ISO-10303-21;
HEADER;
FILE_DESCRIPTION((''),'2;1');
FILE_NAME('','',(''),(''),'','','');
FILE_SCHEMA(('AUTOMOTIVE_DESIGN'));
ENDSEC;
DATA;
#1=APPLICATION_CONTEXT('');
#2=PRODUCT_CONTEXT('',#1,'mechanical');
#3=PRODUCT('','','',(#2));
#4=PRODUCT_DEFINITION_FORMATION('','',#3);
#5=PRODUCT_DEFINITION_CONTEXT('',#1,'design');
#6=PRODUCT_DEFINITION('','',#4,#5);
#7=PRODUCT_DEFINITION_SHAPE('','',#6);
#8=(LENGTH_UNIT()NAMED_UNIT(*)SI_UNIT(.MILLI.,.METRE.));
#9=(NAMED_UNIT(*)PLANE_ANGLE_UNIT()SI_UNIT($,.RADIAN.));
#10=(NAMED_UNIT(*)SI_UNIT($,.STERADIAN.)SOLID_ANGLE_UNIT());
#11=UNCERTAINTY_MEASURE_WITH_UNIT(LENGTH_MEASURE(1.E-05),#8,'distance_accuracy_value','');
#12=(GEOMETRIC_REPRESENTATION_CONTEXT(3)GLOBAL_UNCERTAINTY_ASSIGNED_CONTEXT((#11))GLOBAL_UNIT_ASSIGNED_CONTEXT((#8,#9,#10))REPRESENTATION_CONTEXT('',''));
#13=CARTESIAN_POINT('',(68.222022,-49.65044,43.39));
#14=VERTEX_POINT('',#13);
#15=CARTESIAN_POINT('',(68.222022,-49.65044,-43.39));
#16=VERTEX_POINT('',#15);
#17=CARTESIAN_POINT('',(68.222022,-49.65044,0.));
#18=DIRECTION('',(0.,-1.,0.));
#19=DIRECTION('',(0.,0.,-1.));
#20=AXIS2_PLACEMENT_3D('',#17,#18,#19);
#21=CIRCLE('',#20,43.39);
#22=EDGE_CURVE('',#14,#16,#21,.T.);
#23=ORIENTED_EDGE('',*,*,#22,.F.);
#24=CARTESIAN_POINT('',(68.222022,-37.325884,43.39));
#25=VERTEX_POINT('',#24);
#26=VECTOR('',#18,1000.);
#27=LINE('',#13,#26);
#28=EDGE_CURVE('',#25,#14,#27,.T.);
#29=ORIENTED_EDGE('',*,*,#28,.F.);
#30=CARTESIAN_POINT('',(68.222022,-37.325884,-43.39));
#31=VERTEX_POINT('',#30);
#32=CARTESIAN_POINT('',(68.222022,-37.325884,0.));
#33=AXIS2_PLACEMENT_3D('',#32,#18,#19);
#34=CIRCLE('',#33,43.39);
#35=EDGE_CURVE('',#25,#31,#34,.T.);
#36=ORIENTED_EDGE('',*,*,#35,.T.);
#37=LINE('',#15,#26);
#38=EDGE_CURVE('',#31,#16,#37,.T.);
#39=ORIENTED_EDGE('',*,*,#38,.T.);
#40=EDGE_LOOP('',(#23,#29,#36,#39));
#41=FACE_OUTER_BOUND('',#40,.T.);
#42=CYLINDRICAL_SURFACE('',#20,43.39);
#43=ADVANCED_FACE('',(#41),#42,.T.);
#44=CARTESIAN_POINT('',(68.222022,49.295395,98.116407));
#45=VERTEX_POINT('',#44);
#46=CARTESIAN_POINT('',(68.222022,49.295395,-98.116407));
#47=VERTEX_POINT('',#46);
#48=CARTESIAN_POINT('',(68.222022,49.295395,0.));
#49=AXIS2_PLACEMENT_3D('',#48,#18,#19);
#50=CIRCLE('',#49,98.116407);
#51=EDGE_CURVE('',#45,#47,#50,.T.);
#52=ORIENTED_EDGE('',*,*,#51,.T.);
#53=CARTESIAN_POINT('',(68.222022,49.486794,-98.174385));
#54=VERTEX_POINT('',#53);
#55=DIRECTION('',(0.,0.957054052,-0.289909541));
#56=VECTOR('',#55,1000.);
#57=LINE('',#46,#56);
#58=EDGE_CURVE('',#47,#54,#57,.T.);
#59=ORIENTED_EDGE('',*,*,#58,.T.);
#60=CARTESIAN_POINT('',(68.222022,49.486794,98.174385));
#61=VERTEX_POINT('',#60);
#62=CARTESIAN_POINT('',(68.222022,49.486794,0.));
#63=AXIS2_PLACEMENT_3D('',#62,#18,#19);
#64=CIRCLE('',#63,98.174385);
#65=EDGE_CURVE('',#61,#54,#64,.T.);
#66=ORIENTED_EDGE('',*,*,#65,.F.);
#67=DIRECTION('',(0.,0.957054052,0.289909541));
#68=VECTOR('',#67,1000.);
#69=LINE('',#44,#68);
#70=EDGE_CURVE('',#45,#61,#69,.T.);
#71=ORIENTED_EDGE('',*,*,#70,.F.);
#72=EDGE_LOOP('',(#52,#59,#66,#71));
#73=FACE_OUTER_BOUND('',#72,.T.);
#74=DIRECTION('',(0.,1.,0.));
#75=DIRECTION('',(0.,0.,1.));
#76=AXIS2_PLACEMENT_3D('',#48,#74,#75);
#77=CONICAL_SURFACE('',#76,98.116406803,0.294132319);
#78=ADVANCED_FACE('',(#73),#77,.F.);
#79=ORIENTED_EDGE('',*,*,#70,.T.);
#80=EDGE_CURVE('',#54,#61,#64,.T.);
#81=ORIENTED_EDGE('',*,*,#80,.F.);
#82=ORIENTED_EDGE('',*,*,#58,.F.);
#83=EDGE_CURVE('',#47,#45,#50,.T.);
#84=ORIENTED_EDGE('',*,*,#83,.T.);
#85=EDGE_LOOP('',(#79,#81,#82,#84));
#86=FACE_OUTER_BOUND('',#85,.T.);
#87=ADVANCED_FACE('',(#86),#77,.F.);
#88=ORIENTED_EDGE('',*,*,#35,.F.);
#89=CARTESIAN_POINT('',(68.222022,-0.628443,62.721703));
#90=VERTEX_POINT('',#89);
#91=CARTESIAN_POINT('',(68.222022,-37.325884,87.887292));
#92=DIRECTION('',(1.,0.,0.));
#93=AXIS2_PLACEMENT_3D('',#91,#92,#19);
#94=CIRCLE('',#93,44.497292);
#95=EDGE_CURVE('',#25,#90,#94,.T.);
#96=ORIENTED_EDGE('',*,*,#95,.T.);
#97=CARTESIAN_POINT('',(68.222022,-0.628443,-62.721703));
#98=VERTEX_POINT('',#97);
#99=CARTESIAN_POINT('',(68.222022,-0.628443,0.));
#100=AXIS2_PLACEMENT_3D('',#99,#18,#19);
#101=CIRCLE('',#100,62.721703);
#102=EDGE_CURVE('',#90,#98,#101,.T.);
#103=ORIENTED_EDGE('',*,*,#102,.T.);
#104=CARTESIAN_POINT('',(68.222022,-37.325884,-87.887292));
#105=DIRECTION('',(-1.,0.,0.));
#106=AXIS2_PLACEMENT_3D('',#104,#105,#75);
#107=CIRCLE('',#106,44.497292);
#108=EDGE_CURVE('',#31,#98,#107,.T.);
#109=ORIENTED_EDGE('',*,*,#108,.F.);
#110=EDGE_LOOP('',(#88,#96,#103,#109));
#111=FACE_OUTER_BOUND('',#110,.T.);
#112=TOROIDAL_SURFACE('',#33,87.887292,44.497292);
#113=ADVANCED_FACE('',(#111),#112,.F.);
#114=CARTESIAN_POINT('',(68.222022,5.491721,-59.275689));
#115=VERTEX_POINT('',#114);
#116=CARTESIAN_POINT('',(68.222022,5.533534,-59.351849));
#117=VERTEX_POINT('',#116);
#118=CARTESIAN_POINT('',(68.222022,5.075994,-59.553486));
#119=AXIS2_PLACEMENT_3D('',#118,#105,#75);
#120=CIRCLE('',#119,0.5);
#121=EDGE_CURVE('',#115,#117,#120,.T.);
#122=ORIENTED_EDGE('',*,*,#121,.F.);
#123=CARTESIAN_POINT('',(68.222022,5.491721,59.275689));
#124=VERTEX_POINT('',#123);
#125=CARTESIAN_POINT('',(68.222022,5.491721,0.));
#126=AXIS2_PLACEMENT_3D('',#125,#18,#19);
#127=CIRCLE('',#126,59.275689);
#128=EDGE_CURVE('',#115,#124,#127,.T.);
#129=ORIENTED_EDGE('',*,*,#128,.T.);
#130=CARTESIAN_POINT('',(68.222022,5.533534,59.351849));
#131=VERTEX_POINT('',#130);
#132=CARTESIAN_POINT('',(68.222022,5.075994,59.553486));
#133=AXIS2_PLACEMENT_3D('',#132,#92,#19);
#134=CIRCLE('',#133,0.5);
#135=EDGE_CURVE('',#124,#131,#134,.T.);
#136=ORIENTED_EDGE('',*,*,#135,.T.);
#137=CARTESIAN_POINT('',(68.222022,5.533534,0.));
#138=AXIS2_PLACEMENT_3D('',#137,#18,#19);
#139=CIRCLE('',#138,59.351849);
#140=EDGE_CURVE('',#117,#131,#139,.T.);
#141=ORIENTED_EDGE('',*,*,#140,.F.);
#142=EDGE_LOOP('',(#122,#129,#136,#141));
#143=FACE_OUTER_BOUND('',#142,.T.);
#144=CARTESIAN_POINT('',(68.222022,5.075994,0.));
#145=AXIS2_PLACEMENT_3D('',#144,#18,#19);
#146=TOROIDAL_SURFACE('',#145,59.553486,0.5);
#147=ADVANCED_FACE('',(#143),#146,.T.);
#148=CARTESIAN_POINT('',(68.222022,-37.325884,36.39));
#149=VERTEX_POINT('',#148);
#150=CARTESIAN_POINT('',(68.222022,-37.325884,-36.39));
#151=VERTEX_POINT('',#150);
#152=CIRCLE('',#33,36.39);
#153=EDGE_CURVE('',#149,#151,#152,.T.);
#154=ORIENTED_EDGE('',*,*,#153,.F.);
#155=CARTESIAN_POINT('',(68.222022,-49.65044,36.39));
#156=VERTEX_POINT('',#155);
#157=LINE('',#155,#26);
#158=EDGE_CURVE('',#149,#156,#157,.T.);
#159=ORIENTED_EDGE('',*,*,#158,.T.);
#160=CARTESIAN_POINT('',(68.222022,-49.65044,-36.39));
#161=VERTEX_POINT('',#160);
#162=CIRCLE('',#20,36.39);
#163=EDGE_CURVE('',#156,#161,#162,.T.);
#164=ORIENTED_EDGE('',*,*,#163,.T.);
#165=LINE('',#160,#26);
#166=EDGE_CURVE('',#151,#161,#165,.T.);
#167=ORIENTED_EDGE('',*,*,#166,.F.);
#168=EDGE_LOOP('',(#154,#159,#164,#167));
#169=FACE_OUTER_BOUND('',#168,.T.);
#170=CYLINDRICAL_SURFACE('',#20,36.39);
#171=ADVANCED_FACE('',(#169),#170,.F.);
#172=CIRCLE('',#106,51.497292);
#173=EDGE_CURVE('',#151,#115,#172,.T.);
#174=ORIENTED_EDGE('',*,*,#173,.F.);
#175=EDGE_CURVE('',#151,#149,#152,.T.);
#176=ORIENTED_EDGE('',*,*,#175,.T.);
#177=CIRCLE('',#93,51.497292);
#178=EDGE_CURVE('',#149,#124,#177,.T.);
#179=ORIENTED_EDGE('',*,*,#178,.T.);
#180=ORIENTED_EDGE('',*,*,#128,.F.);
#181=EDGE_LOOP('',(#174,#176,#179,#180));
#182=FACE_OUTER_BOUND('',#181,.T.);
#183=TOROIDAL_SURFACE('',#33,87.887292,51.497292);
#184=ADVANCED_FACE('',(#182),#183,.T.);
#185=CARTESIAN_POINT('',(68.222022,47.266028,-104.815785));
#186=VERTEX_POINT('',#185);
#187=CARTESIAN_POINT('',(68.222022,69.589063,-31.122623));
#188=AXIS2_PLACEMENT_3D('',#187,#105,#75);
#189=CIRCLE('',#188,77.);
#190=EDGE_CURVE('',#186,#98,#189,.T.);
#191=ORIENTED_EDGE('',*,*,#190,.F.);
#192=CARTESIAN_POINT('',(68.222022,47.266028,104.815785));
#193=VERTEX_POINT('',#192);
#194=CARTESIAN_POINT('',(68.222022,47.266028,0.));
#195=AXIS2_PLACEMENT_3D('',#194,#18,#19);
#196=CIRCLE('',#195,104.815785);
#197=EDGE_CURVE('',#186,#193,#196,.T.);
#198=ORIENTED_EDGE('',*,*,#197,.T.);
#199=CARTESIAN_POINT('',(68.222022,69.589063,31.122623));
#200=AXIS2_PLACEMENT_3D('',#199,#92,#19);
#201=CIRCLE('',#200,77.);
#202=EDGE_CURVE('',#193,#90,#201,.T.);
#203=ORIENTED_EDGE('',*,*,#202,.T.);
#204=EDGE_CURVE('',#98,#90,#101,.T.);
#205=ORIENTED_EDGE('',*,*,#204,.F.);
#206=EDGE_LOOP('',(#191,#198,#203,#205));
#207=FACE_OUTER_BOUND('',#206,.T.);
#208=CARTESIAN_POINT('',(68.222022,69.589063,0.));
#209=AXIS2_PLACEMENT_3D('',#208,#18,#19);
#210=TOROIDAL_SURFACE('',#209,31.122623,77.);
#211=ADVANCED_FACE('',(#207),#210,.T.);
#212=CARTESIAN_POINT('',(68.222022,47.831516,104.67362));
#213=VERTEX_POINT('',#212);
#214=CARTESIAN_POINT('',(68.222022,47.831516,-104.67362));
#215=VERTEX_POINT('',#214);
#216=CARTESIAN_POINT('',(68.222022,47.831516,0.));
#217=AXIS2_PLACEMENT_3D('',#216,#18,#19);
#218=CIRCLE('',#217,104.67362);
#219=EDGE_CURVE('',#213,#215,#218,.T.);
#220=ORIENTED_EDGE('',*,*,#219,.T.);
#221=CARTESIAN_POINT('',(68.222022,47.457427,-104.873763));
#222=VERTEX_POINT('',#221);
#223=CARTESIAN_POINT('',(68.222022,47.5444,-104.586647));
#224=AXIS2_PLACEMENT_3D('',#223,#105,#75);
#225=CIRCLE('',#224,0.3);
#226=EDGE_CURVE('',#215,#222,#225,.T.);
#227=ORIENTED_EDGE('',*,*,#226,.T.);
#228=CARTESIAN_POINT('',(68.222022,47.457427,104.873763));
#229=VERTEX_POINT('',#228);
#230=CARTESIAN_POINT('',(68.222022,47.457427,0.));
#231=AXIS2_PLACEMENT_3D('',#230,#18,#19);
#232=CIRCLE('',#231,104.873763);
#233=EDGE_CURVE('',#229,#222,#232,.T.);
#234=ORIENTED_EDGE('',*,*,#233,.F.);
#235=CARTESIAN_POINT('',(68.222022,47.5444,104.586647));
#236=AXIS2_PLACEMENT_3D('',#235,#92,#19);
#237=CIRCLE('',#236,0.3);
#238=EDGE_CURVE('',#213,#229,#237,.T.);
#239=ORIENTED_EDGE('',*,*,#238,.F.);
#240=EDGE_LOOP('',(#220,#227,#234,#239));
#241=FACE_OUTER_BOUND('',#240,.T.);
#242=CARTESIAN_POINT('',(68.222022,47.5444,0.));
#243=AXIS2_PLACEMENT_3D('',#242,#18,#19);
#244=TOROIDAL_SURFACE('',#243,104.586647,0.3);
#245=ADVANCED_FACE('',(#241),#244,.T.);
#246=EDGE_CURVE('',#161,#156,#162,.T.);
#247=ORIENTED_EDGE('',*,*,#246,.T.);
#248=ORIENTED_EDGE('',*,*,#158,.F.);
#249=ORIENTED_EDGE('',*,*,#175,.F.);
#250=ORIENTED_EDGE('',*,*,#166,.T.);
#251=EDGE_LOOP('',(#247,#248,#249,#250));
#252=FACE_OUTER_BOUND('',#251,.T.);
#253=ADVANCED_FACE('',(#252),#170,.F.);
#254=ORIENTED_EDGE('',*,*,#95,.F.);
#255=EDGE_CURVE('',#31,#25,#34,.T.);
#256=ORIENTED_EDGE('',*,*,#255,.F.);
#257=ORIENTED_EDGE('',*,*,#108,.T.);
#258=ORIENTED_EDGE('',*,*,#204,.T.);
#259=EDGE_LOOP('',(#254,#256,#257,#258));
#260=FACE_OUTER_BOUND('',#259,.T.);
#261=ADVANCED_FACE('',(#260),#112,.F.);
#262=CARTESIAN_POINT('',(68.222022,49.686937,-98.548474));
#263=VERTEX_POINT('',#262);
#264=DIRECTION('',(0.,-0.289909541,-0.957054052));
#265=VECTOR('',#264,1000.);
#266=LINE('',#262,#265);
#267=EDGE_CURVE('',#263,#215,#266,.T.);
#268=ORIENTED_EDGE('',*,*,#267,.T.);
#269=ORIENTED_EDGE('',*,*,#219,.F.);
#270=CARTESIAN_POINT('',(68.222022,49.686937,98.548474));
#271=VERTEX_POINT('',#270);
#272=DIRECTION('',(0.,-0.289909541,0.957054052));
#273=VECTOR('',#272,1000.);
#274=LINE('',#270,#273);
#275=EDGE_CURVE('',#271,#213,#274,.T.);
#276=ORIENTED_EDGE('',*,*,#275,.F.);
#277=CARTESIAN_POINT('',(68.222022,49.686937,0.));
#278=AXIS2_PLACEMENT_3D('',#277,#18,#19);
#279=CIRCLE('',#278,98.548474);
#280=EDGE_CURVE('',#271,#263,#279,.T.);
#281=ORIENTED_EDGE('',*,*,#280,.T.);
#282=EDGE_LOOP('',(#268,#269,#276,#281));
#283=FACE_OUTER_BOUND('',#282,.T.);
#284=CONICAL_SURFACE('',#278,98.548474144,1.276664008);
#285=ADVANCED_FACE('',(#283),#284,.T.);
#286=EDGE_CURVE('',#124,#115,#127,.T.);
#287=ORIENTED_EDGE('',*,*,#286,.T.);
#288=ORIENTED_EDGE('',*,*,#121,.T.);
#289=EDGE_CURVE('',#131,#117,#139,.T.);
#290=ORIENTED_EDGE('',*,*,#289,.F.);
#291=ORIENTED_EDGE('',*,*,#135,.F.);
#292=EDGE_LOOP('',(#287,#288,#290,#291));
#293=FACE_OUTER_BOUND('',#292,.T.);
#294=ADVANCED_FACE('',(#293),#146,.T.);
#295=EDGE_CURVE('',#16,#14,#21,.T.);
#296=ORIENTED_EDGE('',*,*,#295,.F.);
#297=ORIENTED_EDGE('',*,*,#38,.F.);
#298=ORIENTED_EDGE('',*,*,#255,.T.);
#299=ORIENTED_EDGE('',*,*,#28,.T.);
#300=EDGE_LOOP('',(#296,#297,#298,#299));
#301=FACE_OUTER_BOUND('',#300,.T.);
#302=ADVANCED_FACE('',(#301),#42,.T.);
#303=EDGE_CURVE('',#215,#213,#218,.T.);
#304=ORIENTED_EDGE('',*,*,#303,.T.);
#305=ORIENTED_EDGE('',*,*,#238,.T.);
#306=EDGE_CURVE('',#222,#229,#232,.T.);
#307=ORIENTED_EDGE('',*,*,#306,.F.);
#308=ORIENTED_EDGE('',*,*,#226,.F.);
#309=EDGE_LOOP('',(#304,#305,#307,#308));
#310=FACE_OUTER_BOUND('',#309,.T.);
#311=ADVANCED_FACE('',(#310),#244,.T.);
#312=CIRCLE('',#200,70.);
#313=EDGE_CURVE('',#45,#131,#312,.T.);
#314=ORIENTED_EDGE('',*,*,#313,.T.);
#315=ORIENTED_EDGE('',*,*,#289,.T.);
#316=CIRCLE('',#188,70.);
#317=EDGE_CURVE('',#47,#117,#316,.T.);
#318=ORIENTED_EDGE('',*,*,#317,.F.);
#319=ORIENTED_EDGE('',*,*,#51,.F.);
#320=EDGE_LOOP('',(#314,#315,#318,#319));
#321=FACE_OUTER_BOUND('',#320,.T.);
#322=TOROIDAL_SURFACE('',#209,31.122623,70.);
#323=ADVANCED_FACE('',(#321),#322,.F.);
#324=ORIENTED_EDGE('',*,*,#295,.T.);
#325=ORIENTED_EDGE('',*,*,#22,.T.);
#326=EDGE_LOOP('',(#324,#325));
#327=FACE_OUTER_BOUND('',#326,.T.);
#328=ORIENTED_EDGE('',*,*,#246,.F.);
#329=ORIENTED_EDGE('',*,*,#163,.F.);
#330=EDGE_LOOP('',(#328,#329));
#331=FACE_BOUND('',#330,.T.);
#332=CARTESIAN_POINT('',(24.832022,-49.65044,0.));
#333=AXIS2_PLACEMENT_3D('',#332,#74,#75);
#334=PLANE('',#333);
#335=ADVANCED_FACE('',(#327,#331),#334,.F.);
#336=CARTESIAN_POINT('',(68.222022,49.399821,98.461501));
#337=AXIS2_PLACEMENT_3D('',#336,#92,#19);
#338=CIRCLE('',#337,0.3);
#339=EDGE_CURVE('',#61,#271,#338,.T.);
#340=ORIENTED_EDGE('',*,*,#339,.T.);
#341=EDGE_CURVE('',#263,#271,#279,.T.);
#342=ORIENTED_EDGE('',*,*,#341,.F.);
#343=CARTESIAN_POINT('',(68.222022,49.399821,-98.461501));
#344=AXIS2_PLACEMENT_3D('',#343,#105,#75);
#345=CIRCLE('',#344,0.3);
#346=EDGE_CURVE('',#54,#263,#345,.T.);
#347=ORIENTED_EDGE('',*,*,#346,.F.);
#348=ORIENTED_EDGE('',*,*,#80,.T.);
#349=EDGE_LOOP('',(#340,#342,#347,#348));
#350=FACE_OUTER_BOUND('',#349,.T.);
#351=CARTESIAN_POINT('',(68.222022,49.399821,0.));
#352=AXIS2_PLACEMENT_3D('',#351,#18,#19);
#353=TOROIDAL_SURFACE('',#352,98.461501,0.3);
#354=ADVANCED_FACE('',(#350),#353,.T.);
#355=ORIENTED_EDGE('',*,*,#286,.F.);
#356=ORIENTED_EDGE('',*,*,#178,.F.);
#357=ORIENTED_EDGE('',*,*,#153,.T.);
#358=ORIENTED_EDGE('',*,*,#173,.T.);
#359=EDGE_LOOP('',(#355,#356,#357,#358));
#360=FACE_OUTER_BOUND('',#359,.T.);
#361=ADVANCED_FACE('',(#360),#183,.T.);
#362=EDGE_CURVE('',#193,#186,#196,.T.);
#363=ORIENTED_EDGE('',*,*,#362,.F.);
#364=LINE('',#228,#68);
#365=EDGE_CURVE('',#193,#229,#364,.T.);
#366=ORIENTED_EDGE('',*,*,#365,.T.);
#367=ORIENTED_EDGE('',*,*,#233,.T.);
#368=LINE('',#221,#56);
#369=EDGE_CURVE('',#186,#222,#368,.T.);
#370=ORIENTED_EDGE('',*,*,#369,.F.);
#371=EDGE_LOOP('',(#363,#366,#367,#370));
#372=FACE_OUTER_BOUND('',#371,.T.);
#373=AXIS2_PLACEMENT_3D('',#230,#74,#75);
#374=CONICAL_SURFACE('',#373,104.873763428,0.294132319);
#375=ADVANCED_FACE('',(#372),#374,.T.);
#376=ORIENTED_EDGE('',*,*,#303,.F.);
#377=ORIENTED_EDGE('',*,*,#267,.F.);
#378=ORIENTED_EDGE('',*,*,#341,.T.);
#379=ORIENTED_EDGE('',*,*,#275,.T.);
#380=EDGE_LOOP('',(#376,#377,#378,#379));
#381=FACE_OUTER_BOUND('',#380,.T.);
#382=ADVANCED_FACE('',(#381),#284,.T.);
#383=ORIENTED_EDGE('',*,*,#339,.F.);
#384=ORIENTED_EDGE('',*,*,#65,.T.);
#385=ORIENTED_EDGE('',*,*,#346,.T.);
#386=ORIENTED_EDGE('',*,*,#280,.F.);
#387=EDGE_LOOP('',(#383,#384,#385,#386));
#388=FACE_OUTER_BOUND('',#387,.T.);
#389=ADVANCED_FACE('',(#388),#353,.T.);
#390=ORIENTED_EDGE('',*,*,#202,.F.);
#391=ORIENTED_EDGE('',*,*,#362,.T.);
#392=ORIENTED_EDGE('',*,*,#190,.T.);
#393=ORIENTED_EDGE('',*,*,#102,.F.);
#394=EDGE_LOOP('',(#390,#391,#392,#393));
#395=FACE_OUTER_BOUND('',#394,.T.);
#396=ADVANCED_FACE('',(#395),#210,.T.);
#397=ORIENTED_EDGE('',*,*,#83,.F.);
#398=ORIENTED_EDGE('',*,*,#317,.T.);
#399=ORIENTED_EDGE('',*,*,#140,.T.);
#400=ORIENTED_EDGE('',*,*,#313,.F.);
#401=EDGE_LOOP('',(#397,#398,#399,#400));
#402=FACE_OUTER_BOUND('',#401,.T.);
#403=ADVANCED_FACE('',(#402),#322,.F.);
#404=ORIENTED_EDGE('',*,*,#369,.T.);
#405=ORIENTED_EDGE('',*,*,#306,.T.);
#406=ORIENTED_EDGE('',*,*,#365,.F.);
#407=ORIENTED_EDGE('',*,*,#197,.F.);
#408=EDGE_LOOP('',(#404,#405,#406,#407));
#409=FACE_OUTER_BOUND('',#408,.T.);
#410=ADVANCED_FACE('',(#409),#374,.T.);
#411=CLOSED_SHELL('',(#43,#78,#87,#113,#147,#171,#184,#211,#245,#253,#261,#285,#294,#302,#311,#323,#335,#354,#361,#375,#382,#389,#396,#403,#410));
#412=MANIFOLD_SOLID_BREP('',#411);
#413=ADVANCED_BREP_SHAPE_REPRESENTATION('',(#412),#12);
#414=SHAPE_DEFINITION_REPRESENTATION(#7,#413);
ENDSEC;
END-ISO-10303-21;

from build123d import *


with BuildPart() as part:
    # Sketch1 → Revolution1 (revolve)
    with BuildSketch(Plane.XY, mode=Mode.PRIVATE) as revolution1_sk:
        with BuildLine():
            Line((31.832021846, -49.650440399), (31.832021846, -37.325883541))
            ThreePointArc((31.832021846, -37.325883541), (25.751638451, -13.050886085), (8.946333163, 5.491721011))
            ThreePointArc((8.946333163, 5.491721011), (8.909163165, 5.51428476), (8.870173321, 5.533533751))
            ThreePointArc((8.870173321, 5.533533751), (-15.299365519, 23.173876843), (-29.894384958, 49.29539517))
            Line((-29.894384958, 49.29539517), (-29.952363221, 49.486793945))
            ThreePointArc((-29.952363221, 49.486793945), (-30.097956714, 49.664342007), (-30.326452298, 49.686937298))
            Line((-30.326452298, 49.686937298), (-36.451598229, 47.831516233))
            ThreePointArc((-36.451598229, 47.831516233), (-36.62914629, 47.685922739), (-36.651741582, 47.457427155))
            Line((-36.651741582, 47.457427155), (-36.593763319, 47.266028379))
            ThreePointArc((-36.593763319, 47.266028379), (-20.737303749, 18.756830634), (5.500318761, -0.628442931))
            ThreePointArc((5.500318761, -0.628442931), (19.703559865, -16.586929303), (24.832021846, -37.325883541))
            Line((24.832021846, -37.325883541), (24.832021846, -49.650440399))
            Line((24.832021846, -49.650440399), (31.832021846, -49.650440399))
        make_face()
    revolve(revolution1_sk.sketch.rotate(Axis((68.222021846, -49.650440399, 0), (0, 1, 0)), 270), axis=Axis((68.222021846, -49.650440399, 0), (0, 1, 0)))


solid = part.part
